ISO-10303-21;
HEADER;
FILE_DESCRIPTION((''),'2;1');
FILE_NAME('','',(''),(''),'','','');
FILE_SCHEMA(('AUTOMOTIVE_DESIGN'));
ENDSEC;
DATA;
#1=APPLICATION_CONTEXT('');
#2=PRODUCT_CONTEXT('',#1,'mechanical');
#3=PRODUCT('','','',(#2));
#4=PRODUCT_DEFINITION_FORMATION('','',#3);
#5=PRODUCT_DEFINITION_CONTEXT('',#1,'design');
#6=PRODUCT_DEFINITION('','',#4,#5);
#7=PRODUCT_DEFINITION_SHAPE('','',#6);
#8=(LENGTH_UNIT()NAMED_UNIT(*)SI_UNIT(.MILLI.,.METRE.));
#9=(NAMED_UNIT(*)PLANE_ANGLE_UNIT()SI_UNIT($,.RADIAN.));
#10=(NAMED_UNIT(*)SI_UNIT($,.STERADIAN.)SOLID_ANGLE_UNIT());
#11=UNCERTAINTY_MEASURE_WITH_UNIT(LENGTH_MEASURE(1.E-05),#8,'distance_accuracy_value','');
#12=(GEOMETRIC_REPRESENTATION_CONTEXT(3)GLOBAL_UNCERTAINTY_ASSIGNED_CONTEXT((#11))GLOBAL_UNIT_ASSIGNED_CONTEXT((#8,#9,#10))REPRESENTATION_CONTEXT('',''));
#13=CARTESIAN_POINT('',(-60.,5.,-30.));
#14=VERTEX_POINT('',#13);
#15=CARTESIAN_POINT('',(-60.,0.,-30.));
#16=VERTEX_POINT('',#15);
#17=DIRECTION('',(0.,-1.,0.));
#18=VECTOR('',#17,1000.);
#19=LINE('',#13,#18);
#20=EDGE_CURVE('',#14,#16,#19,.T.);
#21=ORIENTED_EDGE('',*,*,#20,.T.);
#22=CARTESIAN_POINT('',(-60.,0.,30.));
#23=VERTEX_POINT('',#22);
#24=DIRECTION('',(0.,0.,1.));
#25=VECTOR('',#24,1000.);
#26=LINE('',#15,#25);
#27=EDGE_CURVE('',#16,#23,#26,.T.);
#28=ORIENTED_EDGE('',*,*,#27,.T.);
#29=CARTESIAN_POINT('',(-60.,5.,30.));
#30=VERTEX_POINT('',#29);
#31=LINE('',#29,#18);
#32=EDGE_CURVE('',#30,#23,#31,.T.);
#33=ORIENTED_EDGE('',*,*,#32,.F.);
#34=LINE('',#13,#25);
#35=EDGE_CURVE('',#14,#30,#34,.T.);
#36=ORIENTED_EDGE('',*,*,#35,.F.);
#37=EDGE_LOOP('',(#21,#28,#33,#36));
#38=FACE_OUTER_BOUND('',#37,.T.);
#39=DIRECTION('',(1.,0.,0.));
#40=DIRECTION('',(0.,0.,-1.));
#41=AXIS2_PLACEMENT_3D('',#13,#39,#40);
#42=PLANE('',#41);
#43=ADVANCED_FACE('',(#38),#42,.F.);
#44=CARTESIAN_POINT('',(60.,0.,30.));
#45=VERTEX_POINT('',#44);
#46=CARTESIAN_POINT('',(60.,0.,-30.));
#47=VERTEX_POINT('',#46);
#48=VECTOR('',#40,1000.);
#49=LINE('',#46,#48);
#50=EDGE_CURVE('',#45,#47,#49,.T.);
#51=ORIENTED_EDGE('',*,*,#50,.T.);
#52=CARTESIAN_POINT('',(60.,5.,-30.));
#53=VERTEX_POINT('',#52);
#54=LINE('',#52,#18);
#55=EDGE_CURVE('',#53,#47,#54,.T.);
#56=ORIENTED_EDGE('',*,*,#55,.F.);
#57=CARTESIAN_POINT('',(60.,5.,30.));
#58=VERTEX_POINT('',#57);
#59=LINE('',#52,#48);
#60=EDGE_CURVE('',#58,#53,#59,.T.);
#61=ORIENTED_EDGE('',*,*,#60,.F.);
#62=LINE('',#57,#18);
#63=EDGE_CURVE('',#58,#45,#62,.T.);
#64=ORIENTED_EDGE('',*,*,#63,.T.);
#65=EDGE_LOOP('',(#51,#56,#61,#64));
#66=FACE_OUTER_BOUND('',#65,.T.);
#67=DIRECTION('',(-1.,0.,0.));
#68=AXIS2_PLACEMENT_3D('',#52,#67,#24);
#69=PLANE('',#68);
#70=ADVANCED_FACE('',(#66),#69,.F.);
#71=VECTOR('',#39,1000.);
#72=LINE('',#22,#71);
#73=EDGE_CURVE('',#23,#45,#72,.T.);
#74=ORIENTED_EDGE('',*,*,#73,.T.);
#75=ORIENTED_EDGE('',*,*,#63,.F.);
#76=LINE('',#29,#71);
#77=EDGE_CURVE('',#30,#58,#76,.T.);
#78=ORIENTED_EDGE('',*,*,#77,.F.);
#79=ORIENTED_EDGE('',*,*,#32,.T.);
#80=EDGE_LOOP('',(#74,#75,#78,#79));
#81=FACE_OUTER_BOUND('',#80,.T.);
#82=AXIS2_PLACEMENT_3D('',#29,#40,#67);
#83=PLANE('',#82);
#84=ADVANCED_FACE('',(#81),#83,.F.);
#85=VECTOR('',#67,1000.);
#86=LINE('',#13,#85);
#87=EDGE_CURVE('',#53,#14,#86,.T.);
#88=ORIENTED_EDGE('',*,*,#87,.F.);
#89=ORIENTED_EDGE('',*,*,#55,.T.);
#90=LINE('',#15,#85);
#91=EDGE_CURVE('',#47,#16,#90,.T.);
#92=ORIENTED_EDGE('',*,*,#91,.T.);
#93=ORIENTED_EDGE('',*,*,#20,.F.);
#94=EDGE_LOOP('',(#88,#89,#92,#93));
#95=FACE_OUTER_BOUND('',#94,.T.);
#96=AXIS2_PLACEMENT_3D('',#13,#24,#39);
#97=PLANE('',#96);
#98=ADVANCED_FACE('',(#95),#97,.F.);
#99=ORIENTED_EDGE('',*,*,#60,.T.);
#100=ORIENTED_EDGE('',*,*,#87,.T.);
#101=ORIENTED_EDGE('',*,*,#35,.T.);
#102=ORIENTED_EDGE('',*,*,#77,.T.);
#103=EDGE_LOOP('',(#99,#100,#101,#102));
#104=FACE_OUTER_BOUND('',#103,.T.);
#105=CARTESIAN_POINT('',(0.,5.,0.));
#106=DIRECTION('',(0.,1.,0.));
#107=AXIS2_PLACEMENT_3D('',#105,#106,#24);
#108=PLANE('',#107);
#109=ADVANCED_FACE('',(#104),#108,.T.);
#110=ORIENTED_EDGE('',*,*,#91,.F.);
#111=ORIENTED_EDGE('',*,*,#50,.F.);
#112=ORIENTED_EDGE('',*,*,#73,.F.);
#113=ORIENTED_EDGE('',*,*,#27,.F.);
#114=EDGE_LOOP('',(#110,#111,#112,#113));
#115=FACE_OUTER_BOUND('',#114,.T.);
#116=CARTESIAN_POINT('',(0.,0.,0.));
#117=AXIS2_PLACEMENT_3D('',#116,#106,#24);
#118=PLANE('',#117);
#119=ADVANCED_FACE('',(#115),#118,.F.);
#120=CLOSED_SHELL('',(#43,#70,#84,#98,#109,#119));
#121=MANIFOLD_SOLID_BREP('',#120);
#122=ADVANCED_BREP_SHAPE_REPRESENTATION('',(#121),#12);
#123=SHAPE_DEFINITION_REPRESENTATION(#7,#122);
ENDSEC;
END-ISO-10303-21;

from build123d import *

# Parameters (mm, degrees)
SKETCH1_W           = 120
SKETCH1_H           = 60
BOSS_EXTRUDE1_DEPTH = 5


with BuildPart() as part:
    # Sketch1 → Boss-Extrude1 (new body)
    with BuildSketch(Plane(origin=(0, 0, 0), x_dir=(1, 0, 0), z_dir=(0, 1, 0))):
        Rectangle(SKETCH1_W, SKETCH1_H)
    extrude(amount=BOSS_EXTRUDE1_DEPTH)


solid = part.part
